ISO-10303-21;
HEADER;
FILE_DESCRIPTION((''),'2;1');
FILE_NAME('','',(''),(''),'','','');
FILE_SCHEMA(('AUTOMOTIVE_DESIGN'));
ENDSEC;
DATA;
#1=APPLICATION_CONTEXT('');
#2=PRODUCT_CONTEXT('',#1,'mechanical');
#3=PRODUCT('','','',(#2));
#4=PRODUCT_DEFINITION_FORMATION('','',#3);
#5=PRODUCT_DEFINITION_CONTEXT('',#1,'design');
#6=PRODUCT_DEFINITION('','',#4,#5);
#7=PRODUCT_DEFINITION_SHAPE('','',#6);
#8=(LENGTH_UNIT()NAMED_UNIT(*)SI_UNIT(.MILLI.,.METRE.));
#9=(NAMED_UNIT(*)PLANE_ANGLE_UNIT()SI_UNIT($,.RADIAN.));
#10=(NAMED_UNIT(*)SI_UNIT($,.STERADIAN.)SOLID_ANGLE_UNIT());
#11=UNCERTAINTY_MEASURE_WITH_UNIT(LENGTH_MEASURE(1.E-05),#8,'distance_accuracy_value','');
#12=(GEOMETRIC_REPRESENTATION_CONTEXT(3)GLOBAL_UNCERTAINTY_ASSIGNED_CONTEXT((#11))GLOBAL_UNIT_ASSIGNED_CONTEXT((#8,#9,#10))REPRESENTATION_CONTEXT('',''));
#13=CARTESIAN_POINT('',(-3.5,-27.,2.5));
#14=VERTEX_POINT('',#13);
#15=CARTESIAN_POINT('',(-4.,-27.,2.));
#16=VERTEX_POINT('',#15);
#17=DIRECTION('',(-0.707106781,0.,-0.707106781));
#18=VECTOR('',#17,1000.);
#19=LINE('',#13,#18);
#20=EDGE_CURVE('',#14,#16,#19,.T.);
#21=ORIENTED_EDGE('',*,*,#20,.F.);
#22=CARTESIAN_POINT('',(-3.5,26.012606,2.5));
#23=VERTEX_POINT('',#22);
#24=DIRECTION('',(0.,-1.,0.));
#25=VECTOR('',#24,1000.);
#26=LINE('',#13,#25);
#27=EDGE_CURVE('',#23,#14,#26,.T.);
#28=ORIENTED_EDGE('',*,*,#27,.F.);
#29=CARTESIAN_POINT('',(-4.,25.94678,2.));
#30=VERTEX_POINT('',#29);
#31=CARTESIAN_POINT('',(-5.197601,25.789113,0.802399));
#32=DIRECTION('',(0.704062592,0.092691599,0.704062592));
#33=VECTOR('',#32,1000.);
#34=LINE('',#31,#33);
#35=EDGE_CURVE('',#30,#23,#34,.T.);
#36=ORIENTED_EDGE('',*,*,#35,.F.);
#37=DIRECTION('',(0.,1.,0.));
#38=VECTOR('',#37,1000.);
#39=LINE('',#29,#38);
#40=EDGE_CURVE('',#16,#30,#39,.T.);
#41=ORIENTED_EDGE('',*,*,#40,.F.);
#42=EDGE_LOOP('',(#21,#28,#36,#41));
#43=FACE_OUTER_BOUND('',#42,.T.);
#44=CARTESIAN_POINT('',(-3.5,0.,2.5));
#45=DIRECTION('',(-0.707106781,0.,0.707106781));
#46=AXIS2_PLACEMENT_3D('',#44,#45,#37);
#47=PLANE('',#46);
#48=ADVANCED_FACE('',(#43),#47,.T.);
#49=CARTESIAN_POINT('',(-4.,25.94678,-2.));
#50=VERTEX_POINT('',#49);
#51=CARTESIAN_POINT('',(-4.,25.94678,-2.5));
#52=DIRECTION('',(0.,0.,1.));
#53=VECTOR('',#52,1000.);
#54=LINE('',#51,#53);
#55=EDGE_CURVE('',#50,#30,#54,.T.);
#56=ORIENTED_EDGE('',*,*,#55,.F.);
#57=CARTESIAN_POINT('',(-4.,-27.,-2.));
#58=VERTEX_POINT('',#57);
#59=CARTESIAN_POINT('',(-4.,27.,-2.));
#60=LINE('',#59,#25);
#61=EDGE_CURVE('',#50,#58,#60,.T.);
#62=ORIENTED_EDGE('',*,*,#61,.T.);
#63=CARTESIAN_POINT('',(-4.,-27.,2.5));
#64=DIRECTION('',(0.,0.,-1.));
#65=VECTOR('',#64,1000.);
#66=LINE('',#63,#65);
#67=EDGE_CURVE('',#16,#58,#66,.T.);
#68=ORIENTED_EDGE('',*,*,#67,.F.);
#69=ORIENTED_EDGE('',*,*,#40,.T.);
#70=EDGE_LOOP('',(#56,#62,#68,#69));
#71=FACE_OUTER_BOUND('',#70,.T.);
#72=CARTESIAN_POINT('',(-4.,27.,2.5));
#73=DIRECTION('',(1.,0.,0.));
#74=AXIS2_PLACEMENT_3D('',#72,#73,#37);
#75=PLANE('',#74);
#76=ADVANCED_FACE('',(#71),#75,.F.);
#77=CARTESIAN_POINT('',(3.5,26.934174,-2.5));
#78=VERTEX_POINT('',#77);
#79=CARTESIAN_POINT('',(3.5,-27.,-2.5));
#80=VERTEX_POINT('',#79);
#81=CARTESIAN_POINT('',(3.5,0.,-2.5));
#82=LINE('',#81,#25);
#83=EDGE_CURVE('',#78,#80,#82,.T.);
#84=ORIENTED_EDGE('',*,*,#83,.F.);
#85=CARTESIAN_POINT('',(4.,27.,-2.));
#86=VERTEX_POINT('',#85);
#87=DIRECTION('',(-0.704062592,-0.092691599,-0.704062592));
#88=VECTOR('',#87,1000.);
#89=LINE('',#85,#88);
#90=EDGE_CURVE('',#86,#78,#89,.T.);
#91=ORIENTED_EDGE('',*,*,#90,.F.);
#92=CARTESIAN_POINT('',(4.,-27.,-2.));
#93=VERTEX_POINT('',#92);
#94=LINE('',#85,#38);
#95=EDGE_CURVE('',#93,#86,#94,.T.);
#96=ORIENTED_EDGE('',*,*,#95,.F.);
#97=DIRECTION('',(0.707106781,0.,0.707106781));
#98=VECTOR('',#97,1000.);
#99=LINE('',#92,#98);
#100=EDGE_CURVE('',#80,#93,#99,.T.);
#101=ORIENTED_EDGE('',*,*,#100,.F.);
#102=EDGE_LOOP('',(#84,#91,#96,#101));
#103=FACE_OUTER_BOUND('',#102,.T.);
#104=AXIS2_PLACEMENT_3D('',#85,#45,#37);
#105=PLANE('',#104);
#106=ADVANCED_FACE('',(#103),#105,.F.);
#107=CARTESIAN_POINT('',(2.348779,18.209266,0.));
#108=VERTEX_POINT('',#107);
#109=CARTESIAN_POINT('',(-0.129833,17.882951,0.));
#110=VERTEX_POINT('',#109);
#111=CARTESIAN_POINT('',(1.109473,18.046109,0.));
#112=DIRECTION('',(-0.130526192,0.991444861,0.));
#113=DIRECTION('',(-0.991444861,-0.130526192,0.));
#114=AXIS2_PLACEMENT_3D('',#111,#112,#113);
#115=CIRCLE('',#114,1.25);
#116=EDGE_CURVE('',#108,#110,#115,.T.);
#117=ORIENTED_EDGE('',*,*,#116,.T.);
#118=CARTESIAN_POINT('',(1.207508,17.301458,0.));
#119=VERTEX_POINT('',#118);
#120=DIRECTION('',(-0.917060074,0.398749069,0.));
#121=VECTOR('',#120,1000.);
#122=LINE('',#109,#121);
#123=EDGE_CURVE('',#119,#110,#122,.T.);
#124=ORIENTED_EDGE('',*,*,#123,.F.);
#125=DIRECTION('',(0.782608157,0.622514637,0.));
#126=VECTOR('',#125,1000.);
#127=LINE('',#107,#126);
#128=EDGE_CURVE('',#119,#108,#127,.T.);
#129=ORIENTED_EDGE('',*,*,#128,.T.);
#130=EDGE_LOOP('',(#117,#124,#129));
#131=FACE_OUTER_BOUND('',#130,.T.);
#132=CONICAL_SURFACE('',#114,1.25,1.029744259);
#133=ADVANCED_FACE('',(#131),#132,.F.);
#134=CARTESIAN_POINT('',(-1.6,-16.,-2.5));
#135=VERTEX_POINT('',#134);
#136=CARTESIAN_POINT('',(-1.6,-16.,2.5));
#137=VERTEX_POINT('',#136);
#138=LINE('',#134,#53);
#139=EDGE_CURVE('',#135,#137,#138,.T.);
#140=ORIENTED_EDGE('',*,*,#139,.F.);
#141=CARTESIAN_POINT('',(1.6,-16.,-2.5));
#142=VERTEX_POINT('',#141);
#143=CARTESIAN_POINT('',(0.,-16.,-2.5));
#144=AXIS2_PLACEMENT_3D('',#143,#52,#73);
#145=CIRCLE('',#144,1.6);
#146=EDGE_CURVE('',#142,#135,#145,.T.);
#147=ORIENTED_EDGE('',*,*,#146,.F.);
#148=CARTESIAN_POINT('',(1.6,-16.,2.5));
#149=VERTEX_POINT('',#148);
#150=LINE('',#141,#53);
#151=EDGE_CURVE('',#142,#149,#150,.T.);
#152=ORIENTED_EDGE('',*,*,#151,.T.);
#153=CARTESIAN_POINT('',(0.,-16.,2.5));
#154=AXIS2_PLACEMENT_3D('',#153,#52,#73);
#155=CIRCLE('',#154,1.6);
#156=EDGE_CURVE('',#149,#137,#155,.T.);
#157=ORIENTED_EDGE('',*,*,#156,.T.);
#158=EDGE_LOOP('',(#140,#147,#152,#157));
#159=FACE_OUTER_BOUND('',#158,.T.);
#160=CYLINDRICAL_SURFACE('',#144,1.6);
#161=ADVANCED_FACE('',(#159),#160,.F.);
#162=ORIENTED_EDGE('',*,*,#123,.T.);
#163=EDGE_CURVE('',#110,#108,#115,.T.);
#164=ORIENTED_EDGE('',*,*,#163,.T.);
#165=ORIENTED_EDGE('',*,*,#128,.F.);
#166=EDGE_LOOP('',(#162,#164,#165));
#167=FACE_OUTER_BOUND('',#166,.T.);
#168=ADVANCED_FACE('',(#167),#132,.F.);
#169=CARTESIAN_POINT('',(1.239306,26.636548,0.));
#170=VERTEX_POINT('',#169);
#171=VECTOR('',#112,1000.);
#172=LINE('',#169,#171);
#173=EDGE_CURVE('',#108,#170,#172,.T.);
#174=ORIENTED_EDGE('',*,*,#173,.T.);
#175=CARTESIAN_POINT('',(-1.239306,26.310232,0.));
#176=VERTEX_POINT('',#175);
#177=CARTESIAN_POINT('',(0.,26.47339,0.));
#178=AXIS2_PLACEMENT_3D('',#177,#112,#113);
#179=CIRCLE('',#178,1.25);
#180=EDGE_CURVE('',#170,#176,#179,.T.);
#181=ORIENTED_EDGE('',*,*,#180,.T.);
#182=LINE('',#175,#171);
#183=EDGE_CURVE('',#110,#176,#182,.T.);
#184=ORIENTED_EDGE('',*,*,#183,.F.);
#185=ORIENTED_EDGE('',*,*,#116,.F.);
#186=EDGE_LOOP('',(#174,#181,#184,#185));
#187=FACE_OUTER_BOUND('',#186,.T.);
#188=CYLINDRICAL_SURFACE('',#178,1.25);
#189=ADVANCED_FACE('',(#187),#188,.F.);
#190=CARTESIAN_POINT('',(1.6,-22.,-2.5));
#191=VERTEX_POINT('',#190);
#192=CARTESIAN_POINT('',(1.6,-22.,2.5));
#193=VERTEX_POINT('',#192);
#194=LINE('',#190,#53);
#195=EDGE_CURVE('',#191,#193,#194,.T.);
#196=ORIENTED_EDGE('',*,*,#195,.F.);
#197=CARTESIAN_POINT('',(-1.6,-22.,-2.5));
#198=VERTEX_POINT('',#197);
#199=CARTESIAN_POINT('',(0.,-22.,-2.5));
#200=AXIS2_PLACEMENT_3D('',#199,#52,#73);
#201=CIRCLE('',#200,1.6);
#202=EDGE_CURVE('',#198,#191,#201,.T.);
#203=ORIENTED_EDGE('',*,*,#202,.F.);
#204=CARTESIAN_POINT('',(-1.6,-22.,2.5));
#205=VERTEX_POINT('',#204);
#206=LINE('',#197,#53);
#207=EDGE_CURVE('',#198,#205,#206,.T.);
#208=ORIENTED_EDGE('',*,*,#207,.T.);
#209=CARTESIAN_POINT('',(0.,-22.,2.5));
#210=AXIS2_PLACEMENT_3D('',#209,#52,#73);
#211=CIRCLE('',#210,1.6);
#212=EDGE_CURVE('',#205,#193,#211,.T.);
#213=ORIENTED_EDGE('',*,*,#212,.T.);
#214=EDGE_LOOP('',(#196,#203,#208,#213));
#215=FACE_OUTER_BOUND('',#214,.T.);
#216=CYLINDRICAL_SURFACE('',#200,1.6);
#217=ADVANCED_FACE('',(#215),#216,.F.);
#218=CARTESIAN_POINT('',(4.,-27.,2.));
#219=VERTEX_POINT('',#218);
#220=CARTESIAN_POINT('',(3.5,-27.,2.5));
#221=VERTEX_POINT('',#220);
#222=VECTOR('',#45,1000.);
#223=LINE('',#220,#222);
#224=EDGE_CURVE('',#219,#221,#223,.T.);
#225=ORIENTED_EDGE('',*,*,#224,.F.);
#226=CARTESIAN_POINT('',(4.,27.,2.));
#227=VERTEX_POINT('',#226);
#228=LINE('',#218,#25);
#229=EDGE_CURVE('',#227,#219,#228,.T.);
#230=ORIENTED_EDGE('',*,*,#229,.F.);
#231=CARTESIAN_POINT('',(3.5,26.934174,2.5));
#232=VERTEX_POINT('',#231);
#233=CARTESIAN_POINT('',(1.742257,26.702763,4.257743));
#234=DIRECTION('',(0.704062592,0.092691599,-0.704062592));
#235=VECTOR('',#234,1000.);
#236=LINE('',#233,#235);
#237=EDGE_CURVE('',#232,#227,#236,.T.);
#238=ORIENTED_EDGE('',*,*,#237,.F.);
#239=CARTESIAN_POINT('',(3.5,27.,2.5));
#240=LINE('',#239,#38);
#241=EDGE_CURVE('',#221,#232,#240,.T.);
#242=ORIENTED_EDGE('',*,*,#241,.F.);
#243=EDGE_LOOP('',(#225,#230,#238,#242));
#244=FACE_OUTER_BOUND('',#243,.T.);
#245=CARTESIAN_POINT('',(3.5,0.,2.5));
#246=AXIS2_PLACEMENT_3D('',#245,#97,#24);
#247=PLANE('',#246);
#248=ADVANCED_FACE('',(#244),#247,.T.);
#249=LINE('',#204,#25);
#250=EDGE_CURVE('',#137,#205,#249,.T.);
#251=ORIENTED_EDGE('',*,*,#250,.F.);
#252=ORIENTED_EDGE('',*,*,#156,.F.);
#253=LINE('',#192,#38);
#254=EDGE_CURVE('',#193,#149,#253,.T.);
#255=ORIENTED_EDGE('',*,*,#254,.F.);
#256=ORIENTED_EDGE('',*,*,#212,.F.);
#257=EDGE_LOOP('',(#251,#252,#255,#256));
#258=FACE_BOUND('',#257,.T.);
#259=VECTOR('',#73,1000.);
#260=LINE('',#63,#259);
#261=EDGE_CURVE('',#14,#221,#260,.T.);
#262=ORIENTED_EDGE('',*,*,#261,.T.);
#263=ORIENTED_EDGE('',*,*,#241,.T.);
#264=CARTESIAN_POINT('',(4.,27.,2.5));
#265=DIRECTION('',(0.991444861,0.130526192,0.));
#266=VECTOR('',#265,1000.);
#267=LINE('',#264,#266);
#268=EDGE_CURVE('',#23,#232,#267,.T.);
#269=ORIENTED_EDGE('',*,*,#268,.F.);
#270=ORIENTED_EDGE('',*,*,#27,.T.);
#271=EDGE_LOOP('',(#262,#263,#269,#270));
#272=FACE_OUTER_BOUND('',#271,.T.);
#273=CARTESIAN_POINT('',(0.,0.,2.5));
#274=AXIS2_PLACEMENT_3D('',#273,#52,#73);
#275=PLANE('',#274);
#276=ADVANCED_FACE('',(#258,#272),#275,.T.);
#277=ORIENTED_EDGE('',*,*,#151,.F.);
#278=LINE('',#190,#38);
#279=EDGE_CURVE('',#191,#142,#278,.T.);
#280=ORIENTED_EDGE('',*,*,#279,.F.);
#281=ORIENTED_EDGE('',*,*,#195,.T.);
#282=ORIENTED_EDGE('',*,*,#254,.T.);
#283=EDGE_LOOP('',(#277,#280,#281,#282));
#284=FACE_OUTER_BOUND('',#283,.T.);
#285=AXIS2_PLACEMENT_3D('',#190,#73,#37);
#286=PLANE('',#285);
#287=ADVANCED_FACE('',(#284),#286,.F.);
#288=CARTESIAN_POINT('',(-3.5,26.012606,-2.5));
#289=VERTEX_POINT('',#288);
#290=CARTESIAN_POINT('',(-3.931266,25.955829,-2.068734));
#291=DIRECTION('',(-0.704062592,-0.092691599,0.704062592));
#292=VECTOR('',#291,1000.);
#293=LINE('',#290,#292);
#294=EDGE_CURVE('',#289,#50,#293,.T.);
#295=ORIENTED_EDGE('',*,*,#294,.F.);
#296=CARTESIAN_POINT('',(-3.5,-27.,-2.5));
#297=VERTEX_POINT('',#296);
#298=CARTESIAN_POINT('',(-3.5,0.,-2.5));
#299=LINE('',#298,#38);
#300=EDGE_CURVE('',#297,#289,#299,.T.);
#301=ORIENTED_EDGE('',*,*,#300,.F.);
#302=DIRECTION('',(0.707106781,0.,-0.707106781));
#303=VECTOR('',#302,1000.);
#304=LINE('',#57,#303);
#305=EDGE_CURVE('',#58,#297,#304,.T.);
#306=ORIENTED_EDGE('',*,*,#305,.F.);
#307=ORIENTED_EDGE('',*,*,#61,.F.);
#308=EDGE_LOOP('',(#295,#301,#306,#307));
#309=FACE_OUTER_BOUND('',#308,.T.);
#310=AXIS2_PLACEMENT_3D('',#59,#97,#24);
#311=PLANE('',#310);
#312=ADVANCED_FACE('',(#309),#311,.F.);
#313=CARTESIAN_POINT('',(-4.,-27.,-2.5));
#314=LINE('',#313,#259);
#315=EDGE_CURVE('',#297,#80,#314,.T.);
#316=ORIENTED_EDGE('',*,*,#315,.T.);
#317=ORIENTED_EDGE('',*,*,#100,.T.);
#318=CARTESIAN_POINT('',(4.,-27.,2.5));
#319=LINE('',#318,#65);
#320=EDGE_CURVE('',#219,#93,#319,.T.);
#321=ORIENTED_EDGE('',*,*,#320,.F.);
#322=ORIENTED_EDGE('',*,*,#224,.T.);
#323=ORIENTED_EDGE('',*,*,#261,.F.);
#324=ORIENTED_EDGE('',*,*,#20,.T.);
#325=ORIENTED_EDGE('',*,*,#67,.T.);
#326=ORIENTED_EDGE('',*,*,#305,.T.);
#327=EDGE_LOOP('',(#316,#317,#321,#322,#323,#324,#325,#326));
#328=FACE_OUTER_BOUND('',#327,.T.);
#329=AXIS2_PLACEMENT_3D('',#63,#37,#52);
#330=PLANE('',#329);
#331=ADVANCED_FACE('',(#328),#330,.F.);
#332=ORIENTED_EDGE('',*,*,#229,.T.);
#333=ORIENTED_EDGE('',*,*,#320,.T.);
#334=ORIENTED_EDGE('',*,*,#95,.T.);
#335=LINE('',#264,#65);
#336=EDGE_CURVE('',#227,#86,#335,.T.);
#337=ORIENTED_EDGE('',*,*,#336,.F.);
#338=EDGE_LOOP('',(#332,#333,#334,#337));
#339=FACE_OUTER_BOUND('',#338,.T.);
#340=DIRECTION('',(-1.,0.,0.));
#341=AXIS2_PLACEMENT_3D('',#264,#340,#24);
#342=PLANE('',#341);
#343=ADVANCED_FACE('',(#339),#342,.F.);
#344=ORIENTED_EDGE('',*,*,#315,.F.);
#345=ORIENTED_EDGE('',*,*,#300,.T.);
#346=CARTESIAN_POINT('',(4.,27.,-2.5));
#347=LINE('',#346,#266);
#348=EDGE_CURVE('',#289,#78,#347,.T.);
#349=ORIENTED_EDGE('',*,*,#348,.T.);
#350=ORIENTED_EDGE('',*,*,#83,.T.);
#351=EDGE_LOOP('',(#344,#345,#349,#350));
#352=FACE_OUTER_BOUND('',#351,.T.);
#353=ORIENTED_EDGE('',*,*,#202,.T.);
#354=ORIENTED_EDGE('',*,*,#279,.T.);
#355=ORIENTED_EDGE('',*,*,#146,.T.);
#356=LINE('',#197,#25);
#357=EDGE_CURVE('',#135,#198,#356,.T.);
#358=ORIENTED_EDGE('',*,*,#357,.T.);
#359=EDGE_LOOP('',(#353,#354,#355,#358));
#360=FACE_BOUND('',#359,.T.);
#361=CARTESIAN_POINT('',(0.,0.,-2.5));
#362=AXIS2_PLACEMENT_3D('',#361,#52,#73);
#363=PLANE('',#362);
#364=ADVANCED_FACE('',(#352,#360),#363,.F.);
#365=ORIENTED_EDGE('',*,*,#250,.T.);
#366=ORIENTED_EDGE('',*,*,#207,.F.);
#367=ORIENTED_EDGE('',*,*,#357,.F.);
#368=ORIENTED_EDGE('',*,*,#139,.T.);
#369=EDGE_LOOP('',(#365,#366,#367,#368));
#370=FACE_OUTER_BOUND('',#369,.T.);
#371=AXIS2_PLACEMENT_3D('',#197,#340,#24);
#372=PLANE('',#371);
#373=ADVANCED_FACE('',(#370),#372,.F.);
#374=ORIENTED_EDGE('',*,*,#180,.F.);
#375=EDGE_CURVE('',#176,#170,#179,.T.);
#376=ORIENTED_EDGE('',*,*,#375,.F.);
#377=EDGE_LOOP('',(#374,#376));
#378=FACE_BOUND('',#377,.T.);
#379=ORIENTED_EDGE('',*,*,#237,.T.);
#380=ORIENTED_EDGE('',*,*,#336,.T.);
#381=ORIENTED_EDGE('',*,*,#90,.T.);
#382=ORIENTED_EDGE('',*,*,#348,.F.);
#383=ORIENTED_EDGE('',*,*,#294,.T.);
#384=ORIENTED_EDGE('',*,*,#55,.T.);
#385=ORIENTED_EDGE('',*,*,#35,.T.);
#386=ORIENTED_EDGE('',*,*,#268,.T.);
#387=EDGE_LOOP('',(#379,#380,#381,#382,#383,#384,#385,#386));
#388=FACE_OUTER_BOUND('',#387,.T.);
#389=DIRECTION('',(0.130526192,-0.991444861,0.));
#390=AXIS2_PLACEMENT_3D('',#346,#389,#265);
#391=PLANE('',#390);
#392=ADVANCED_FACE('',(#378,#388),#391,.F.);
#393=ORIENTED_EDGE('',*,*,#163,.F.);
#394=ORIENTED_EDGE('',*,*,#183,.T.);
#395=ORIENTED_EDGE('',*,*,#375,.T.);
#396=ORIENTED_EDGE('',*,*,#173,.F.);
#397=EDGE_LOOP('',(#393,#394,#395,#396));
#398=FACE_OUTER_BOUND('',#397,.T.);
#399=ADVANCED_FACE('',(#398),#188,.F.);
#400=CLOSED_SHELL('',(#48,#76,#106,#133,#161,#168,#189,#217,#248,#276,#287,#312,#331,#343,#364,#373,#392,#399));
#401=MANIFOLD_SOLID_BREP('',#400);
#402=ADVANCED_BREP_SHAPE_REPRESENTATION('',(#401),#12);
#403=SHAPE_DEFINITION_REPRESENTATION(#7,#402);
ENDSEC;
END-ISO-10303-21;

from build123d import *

# Parameters (mm, degrees)
SKETCH1_W             = 8
SKETCH1_H             = 54
BOSS_EXTRUDE1_DEPTH   = 2.5
CUT_EXTRUDE1_DEPTH    = 28.748873851
M3_TAPPED_HOLE1_D     = 2.5
M3_TAPPED_HOLE1_DEPTH = 8.5
M3_TAPPED_HOLE1_TIP   = 0.751075774
CUT_EXTRUDE2_DEPTH    = 28.748873851
CHAMFER1_SIZE         = 0.5


with BuildPart() as part:
    # Sketch1 → Boss-Extrude1 (new, symmetric)
    with BuildSketch(Plane.XY):
        Rectangle(SKETCH1_W, SKETCH1_H)
    extrude(amount=BOSS_EXTRUDE1_DEPTH, both=True)

    # Sketch2 → Cut-Extrude1 (cut, through all)
    with BuildSketch(Plane.XY.offset(2.5)):
        Polygon((4, 27), (-4, 27), (-4, 25.946780019), align=None)
    extrude(amount=-CUT_EXTRUDE1_DEPTH, mode=Mode.SUBTRACT)

    # M3 Tapped Hole1
    with Locations(Plane(origin=(-3.425908761, 26.022360565, 0), x_dir=(0.9914448613738103, 0.13052619222005266, 0), z_dir=(-0.13052619222005266, 0.9914448613738103, 0))):
        with Locations((3.455470793, 0)):
            Hole(M3_TAPPED_HOLE1_D / 2, depth=M3_TAPPED_HOLE1_DEPTH)
            with Locations((0, 0, -(M3_TAPPED_HOLE1_DEPTH + M3_TAPPED_HOLE1_TIP / 2))):  # 118° drill point
                Cone(0, M3_TAPPED_HOLE1_D / 2, M3_TAPPED_HOLE1_TIP, mode=Mode.SUBTRACT)

    # Sketch5 → Cut-Extrude2 (cut, through all)
    with BuildSketch(Plane.XY.offset(2.5)):
        with BuildLine():
            Line((-1.6, -22), (-1.6, -16))
            ThreePointArc((-1.6, -16), (0, -14.4), (1.6, -16))
            Line((1.6, -16), (1.6, -22))
            ThreePointArc((1.6, -22), (0, -23.6), (-1.6, -22))
        make_face()
    extrude(amount=-CUT_EXTRUDE2_DEPTH, mode=Mode.SUBTRACT)

    # Chamfer1
    chamfer1_edges = [part.edges().sort_by_distance(p)[0] for p in [
        (-4, -0.52660999, -2.5),
        (-4, -0.52660999, 2.5),
        (4, 0, 2.5),
        (4, 0, -2.5),
    ]]
    chamfer(chamfer1_edges, length=CHAMFER1_SIZE)


solid = part.part
